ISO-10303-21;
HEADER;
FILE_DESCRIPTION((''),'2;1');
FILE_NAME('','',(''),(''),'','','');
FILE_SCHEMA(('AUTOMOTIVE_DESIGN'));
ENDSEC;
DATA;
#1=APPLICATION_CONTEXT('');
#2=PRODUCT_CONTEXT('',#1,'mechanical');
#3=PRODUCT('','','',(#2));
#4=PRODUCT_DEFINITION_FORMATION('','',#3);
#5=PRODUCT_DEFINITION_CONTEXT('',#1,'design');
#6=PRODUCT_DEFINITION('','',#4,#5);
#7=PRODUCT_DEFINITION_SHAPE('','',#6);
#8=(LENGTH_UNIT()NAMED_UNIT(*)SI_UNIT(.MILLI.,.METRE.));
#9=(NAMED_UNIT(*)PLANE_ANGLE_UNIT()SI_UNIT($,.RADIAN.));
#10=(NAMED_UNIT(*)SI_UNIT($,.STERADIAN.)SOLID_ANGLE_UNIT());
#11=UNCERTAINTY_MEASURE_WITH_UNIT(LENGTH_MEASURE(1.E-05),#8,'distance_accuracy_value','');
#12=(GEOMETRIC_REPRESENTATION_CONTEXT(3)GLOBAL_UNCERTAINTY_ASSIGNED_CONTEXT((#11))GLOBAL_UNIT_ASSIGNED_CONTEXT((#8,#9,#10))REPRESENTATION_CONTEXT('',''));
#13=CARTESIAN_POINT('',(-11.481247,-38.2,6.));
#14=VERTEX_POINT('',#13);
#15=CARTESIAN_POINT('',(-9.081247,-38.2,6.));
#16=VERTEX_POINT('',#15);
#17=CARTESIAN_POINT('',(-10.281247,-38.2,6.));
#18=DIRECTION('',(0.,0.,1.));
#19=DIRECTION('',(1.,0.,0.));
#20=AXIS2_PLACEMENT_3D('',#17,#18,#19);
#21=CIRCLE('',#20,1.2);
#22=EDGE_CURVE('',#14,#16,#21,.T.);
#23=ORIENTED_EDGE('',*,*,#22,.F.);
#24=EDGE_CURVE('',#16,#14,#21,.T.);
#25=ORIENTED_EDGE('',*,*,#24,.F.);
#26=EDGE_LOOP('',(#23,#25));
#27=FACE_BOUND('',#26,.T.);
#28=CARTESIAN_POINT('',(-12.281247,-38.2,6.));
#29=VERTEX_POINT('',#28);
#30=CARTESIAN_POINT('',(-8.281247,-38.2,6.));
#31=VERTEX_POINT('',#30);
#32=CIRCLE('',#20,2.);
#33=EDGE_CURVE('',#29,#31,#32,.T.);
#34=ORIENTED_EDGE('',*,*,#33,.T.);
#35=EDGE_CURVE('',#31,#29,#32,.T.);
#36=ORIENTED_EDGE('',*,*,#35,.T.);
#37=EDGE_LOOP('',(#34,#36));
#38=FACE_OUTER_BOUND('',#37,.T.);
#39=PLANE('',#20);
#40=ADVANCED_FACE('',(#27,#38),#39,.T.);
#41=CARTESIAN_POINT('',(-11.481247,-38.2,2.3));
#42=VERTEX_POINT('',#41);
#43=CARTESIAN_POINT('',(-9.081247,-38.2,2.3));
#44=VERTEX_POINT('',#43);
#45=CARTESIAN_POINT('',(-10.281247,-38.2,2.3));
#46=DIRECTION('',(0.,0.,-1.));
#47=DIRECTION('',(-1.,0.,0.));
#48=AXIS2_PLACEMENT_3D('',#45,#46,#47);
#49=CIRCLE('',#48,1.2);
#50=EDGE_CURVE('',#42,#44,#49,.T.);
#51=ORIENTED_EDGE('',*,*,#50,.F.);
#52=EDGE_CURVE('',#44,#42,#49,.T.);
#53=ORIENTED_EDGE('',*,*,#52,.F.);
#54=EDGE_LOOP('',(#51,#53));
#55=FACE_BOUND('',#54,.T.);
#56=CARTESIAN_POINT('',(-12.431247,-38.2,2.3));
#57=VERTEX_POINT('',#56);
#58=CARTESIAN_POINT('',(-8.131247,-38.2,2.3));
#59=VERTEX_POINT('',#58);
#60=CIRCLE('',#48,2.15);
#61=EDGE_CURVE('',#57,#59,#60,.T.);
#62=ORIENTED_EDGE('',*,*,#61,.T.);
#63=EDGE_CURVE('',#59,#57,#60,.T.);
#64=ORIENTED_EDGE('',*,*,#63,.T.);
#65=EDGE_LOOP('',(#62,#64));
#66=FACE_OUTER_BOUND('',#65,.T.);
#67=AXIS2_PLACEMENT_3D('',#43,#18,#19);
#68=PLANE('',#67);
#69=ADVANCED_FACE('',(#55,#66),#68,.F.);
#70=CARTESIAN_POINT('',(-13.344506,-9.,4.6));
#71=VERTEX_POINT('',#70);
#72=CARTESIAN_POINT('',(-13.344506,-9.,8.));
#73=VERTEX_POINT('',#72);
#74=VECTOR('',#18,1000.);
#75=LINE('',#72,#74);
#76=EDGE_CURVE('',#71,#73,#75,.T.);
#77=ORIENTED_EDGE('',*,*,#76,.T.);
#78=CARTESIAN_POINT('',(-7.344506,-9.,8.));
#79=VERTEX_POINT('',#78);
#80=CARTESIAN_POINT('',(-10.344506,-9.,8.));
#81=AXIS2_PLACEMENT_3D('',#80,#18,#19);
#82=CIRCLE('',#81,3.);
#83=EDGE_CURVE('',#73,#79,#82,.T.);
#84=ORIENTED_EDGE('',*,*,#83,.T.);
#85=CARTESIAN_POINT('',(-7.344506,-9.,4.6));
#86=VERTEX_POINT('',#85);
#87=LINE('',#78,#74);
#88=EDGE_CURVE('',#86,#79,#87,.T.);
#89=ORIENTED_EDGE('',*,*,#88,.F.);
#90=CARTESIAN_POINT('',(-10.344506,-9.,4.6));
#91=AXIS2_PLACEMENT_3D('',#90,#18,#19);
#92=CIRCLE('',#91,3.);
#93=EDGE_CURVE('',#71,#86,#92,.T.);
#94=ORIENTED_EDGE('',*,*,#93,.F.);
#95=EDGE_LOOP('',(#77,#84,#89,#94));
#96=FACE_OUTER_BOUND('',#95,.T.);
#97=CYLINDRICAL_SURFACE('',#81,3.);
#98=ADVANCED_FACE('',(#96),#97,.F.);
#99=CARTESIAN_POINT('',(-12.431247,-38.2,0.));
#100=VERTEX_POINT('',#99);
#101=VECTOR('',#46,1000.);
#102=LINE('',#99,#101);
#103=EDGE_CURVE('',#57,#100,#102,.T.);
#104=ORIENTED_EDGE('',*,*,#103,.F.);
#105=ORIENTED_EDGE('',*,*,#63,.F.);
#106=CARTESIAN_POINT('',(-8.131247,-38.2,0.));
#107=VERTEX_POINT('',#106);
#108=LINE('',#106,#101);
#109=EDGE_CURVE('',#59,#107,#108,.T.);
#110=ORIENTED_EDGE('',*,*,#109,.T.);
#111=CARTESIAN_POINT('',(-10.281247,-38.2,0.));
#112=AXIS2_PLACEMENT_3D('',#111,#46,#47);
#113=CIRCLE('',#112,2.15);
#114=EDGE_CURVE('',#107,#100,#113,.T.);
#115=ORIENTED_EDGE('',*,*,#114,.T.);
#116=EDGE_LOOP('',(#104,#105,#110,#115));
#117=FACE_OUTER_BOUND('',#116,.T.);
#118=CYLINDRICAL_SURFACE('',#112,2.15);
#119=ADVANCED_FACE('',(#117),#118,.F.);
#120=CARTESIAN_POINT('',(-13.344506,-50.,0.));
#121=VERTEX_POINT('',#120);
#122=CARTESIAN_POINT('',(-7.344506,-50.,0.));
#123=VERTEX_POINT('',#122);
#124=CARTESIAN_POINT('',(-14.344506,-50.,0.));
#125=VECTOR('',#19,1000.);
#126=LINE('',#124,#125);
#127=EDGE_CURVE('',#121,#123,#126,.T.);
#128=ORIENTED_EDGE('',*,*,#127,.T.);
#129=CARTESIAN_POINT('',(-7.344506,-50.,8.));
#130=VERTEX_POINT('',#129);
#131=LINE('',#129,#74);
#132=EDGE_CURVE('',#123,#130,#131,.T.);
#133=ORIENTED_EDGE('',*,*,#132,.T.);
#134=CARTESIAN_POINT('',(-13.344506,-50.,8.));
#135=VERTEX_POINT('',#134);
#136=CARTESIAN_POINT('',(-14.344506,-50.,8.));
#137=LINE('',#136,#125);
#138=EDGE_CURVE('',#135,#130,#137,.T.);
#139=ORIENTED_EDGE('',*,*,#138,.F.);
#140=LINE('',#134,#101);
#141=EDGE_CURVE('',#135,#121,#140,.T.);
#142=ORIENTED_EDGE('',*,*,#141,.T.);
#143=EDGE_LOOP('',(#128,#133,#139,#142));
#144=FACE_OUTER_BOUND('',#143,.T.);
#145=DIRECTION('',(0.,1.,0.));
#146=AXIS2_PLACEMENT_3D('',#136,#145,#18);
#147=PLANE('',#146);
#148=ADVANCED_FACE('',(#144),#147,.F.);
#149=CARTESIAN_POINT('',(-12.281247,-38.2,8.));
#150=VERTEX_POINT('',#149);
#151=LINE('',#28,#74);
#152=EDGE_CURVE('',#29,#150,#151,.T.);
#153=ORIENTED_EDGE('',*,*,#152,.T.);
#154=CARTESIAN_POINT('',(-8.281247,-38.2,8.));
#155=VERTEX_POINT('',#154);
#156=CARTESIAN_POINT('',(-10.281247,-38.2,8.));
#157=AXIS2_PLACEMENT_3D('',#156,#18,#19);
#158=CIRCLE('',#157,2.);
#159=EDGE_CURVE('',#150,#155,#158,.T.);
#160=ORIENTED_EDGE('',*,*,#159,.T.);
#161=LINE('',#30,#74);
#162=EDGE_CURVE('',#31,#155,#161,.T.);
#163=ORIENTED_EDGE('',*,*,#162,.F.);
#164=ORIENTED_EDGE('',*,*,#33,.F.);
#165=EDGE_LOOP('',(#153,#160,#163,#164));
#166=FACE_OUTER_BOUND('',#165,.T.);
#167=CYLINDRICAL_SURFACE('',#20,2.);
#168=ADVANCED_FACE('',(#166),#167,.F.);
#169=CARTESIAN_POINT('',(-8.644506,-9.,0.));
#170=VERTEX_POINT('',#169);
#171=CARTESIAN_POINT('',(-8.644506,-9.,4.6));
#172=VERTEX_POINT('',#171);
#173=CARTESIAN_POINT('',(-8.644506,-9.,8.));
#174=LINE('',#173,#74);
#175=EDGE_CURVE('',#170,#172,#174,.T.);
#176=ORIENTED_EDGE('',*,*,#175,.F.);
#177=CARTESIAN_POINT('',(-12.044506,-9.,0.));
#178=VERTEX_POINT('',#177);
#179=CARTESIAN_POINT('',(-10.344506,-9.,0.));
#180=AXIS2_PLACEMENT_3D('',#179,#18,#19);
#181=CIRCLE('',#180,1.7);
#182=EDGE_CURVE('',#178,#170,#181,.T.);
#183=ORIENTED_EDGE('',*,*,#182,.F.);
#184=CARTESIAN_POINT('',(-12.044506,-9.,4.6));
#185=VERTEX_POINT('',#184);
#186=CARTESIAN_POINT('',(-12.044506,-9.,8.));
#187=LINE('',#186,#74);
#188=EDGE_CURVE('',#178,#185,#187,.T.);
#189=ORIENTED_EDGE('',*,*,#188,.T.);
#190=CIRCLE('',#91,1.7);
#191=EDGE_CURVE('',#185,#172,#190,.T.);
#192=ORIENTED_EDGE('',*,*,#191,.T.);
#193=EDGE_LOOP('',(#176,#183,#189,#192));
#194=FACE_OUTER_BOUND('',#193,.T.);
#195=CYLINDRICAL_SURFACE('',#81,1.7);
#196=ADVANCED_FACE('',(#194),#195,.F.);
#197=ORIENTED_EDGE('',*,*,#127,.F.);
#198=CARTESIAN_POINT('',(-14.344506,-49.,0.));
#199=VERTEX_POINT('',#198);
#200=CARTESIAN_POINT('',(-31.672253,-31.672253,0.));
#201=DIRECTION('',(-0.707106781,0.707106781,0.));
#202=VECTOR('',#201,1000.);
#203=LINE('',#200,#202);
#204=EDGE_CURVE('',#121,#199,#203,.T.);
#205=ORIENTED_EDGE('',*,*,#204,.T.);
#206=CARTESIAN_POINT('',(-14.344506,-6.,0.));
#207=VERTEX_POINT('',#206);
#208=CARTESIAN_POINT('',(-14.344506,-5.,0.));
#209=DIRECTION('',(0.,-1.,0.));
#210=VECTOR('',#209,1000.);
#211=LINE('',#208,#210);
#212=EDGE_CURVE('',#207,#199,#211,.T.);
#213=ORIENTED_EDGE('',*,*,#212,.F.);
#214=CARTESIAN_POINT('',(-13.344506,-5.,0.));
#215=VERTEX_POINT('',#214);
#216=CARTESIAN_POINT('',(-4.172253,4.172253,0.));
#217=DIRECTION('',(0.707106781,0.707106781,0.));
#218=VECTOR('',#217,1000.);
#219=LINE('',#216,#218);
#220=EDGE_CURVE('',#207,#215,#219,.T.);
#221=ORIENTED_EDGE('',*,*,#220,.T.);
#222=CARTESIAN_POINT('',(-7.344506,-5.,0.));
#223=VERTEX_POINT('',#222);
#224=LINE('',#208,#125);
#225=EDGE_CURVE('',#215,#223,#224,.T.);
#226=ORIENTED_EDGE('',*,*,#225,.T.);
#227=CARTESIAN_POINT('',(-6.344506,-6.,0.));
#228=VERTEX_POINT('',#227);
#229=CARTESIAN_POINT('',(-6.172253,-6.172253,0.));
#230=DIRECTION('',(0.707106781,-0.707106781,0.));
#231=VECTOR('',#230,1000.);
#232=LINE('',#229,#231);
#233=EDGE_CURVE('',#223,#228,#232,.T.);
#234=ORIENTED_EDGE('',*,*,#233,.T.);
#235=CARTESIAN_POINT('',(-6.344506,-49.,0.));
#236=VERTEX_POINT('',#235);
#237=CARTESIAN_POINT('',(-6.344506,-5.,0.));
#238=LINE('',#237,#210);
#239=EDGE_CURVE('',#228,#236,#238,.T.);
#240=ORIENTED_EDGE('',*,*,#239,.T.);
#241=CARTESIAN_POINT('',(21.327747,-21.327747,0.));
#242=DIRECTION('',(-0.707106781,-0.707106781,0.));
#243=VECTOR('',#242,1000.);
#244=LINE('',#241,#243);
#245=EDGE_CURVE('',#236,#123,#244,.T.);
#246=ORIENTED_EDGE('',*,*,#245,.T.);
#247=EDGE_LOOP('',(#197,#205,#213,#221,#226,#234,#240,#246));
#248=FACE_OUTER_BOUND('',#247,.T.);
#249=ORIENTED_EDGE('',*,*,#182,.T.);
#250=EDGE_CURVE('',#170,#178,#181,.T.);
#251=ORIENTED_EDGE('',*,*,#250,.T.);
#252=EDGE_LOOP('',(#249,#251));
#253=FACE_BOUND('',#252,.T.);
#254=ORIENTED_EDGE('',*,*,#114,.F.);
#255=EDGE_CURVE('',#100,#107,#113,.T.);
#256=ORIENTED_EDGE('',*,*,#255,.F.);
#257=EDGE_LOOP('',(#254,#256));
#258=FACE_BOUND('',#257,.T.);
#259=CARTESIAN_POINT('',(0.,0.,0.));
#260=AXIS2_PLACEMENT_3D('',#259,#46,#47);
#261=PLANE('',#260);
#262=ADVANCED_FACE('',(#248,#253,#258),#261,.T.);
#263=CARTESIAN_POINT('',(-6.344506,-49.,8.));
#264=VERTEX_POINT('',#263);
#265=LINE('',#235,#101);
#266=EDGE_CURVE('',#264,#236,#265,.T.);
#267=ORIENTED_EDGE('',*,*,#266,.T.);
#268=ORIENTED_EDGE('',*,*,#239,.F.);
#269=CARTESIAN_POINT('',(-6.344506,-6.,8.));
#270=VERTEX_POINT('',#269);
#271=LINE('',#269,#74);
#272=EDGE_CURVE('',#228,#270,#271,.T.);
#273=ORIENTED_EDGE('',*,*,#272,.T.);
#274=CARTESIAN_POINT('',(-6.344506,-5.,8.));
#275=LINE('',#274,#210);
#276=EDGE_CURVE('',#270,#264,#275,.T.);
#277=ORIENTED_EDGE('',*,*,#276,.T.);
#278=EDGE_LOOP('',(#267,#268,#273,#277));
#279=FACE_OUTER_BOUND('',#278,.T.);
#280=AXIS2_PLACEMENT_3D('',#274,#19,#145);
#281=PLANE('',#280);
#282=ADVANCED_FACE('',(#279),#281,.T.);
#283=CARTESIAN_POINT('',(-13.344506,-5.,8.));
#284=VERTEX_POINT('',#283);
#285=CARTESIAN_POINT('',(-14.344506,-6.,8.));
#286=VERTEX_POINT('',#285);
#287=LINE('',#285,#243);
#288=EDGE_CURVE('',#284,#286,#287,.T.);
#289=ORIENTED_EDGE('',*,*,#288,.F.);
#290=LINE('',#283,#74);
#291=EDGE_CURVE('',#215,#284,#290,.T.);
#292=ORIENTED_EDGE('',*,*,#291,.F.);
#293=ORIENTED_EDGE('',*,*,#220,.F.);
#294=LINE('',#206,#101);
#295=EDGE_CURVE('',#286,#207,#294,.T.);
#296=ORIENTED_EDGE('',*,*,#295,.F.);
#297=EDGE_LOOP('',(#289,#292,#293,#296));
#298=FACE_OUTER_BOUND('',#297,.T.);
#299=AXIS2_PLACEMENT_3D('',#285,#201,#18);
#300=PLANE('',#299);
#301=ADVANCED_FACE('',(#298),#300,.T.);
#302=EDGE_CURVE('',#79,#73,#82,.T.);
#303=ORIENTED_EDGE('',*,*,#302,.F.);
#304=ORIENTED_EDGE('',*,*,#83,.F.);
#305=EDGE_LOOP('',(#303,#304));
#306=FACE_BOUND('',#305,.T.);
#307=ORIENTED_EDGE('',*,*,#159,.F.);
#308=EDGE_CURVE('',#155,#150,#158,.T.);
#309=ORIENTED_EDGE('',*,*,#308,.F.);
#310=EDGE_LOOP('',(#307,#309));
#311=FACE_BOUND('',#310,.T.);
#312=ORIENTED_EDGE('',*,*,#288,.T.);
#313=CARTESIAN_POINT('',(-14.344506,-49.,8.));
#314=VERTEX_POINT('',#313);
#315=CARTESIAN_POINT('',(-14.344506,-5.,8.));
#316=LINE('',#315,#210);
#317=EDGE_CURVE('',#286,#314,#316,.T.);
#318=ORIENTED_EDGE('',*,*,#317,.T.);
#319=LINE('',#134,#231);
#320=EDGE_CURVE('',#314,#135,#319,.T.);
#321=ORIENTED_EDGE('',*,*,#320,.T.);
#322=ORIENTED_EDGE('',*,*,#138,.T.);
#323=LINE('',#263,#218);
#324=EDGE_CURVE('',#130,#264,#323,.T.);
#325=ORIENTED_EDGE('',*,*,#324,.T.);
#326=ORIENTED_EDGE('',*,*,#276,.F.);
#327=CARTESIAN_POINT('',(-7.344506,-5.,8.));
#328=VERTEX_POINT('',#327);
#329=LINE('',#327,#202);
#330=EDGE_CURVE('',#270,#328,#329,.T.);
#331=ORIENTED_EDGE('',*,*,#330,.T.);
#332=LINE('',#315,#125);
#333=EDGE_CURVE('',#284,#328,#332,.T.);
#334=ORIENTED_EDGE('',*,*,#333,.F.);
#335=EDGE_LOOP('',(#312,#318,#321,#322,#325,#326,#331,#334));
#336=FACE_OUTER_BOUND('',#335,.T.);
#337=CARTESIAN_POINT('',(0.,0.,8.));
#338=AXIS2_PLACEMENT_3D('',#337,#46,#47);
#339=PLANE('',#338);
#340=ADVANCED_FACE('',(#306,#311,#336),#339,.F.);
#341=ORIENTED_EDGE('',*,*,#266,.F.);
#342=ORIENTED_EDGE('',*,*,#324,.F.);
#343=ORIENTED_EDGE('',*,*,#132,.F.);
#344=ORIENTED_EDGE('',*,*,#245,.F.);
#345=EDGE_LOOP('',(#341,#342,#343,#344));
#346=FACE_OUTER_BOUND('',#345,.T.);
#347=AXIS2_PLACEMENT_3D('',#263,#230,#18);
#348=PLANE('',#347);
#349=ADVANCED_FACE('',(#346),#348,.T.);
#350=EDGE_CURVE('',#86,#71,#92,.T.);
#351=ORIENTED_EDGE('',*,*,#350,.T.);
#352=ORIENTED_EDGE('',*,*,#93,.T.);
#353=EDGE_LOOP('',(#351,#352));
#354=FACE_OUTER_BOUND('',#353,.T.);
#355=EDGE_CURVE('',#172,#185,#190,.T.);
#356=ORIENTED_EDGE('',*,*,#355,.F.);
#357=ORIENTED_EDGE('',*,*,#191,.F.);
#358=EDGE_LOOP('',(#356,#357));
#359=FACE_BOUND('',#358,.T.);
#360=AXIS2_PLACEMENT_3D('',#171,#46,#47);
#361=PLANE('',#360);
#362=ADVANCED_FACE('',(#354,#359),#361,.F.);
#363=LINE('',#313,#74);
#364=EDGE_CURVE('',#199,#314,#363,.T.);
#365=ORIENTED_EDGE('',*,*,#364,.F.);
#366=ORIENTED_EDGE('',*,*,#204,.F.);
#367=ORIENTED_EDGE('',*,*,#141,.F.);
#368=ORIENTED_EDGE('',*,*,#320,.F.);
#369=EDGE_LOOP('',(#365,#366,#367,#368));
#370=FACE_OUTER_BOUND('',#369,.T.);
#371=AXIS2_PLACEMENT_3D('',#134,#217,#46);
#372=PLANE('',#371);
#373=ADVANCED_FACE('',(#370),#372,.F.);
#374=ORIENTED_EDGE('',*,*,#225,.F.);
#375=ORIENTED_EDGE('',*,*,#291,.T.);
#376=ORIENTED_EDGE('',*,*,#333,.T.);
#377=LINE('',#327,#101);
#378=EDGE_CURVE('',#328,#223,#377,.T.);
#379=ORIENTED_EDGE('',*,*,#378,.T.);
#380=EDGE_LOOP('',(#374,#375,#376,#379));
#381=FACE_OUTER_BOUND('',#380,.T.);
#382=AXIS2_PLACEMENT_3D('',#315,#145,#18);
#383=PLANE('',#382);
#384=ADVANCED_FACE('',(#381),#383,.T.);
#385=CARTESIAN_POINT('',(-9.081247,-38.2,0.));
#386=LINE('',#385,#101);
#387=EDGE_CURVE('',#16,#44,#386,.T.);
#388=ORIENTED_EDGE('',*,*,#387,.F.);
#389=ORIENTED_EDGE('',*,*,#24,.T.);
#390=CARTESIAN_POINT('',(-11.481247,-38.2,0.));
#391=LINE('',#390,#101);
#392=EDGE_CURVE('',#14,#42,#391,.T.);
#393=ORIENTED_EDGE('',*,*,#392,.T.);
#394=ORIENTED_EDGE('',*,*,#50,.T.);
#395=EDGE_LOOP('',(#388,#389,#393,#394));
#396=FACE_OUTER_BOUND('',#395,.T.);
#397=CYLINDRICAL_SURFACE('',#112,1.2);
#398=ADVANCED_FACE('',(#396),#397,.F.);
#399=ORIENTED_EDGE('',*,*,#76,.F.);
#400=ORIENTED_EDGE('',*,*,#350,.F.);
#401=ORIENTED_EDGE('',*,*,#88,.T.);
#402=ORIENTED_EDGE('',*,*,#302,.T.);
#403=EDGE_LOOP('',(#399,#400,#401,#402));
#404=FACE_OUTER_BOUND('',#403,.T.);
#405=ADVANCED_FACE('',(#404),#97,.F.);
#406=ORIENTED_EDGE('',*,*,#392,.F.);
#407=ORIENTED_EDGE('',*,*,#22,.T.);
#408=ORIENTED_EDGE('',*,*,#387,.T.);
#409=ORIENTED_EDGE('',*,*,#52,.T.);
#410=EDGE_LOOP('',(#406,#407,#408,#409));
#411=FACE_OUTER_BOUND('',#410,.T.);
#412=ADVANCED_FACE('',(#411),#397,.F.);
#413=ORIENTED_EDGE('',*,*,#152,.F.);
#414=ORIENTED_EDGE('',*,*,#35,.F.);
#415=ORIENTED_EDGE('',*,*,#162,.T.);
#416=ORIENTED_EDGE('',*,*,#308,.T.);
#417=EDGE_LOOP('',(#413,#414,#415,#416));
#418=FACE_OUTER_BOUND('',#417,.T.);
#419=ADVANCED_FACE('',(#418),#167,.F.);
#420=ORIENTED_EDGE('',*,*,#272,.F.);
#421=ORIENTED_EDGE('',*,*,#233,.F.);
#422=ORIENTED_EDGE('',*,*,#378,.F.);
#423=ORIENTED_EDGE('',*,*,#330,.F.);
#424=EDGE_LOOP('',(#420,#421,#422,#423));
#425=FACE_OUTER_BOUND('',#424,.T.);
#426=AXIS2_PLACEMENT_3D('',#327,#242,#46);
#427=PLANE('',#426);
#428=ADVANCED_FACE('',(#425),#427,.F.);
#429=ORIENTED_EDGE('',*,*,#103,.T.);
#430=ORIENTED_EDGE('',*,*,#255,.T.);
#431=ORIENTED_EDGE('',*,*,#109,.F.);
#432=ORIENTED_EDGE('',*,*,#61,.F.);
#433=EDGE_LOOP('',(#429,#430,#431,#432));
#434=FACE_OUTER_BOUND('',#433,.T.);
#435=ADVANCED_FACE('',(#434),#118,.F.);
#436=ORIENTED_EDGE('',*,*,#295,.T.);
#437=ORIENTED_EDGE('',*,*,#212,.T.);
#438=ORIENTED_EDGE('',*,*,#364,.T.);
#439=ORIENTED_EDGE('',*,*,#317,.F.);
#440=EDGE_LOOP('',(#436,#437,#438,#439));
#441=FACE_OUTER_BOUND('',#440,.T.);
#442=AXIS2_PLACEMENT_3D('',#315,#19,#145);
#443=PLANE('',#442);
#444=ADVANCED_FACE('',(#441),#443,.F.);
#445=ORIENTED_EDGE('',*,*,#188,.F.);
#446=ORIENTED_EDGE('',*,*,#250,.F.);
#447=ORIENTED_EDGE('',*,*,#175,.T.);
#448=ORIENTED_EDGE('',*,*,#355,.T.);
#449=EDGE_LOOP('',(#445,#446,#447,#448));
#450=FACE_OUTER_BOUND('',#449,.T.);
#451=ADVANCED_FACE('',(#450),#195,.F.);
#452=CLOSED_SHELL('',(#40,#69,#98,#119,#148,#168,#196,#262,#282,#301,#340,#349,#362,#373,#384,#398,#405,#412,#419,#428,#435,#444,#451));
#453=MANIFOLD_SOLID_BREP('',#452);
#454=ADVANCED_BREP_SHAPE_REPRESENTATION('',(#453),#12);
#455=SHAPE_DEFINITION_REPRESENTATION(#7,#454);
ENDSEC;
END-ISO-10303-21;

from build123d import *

# Parameters (mm, degrees)
SKETCH1_W                                           = 8
SKETCH1_H                                           = 45
BOSS_EXTRUDE1_DEPTH                                 = 8
HOLE_SIZE_PER_SOCKET_HEAD_CAP_SCREW_TYP_D           = 3.4
HOLE_SIZE_PER_SOCKET_HEAD_CAP_SCREW_TYP_CBORE_D     = 6
HOLE_SIZE_PER_SOCKET_HEAD_CAP_SCREW_TYP_CBORE_DEPTH = 3.4
SKETCH2_R                                           = 2
CUT_EXTRUDE1_DEPTH                                  = 2
HOLE_SIZE_PER_SOCKET_HEAD_CAP_SCREW_2_D             = 2.4
HOLE_SIZE_PER_SOCKET_HEAD_CAP_SCREW_2_CBORE_D       = 4.3
HOLE_SIZE_PER_SOCKET_HEAD_CAP_SCREW_2_CBORE_DEPTH   = 2.3
CHAMFER1_SIZE                                       = 1


with BuildPart() as part:
    # Sketch1 → Boss-Extrude1 (new body)
    with BuildSketch(Plane.XY):
        with Locations((-10.344506296, -27.5)):
            Rectangle(SKETCH1_W, SKETCH1_H)
    extrude(amount=BOSS_EXTRUDE1_DEPTH)

    # Hole size _per socket head cap screw typ (through all)
    with Locations(Plane(origin=(-10.344506296, -9, 8), x_dir=(1, 0, 0), z_dir=(0, 0, 1))):
        with Locations((0, 0)):
            CounterBoreHole(HOLE_SIZE_PER_SOCKET_HEAD_CAP_SCREW_TYP_D / 2, HOLE_SIZE_PER_SOCKET_HEAD_CAP_SCREW_TYP_CBORE_D / 2, HOLE_SIZE_PER_SOCKET_HEAD_CAP_SCREW_TYP_CBORE_DEPTH)

    # Sketch2 → Cut-Extrude1 (cut)
    with BuildSketch(Plane.XY.offset(8)):
        with Locations((-10.281246694, -38.2)):
            Circle(SKETCH2_R)
    extrude(amount=-CUT_EXTRUDE1_DEPTH, mode=Mode.SUBTRACT)

    # Hole size _per socket head cap screw 2 (through all)
    with Locations(Plane(origin=(-10.281246694, -38.2, 0), x_dir=(-1, 0, 0), z_dir=(0, 0, -1))):
        with Locations((0, 0)):
            CounterBoreHole(HOLE_SIZE_PER_SOCKET_HEAD_CAP_SCREW_2_D / 2, HOLE_SIZE_PER_SOCKET_HEAD_CAP_SCREW_2_CBORE_D / 2, HOLE_SIZE_PER_SOCKET_HEAD_CAP_SCREW_2_CBORE_DEPTH)

    # Chamfer1
    chamfer1_edges = [part.edges().sort_by_distance(p)[0] for p in [
        (-14.344506296, -5, 4),
        (-14.344506296, -50, 4),
        (-6.344506296, -50, 4),
        (-6.344506296, -5, 4),
    ]]
    chamfer(chamfer1_edges, length=CHAMFER1_SIZE)


solid = part.part
